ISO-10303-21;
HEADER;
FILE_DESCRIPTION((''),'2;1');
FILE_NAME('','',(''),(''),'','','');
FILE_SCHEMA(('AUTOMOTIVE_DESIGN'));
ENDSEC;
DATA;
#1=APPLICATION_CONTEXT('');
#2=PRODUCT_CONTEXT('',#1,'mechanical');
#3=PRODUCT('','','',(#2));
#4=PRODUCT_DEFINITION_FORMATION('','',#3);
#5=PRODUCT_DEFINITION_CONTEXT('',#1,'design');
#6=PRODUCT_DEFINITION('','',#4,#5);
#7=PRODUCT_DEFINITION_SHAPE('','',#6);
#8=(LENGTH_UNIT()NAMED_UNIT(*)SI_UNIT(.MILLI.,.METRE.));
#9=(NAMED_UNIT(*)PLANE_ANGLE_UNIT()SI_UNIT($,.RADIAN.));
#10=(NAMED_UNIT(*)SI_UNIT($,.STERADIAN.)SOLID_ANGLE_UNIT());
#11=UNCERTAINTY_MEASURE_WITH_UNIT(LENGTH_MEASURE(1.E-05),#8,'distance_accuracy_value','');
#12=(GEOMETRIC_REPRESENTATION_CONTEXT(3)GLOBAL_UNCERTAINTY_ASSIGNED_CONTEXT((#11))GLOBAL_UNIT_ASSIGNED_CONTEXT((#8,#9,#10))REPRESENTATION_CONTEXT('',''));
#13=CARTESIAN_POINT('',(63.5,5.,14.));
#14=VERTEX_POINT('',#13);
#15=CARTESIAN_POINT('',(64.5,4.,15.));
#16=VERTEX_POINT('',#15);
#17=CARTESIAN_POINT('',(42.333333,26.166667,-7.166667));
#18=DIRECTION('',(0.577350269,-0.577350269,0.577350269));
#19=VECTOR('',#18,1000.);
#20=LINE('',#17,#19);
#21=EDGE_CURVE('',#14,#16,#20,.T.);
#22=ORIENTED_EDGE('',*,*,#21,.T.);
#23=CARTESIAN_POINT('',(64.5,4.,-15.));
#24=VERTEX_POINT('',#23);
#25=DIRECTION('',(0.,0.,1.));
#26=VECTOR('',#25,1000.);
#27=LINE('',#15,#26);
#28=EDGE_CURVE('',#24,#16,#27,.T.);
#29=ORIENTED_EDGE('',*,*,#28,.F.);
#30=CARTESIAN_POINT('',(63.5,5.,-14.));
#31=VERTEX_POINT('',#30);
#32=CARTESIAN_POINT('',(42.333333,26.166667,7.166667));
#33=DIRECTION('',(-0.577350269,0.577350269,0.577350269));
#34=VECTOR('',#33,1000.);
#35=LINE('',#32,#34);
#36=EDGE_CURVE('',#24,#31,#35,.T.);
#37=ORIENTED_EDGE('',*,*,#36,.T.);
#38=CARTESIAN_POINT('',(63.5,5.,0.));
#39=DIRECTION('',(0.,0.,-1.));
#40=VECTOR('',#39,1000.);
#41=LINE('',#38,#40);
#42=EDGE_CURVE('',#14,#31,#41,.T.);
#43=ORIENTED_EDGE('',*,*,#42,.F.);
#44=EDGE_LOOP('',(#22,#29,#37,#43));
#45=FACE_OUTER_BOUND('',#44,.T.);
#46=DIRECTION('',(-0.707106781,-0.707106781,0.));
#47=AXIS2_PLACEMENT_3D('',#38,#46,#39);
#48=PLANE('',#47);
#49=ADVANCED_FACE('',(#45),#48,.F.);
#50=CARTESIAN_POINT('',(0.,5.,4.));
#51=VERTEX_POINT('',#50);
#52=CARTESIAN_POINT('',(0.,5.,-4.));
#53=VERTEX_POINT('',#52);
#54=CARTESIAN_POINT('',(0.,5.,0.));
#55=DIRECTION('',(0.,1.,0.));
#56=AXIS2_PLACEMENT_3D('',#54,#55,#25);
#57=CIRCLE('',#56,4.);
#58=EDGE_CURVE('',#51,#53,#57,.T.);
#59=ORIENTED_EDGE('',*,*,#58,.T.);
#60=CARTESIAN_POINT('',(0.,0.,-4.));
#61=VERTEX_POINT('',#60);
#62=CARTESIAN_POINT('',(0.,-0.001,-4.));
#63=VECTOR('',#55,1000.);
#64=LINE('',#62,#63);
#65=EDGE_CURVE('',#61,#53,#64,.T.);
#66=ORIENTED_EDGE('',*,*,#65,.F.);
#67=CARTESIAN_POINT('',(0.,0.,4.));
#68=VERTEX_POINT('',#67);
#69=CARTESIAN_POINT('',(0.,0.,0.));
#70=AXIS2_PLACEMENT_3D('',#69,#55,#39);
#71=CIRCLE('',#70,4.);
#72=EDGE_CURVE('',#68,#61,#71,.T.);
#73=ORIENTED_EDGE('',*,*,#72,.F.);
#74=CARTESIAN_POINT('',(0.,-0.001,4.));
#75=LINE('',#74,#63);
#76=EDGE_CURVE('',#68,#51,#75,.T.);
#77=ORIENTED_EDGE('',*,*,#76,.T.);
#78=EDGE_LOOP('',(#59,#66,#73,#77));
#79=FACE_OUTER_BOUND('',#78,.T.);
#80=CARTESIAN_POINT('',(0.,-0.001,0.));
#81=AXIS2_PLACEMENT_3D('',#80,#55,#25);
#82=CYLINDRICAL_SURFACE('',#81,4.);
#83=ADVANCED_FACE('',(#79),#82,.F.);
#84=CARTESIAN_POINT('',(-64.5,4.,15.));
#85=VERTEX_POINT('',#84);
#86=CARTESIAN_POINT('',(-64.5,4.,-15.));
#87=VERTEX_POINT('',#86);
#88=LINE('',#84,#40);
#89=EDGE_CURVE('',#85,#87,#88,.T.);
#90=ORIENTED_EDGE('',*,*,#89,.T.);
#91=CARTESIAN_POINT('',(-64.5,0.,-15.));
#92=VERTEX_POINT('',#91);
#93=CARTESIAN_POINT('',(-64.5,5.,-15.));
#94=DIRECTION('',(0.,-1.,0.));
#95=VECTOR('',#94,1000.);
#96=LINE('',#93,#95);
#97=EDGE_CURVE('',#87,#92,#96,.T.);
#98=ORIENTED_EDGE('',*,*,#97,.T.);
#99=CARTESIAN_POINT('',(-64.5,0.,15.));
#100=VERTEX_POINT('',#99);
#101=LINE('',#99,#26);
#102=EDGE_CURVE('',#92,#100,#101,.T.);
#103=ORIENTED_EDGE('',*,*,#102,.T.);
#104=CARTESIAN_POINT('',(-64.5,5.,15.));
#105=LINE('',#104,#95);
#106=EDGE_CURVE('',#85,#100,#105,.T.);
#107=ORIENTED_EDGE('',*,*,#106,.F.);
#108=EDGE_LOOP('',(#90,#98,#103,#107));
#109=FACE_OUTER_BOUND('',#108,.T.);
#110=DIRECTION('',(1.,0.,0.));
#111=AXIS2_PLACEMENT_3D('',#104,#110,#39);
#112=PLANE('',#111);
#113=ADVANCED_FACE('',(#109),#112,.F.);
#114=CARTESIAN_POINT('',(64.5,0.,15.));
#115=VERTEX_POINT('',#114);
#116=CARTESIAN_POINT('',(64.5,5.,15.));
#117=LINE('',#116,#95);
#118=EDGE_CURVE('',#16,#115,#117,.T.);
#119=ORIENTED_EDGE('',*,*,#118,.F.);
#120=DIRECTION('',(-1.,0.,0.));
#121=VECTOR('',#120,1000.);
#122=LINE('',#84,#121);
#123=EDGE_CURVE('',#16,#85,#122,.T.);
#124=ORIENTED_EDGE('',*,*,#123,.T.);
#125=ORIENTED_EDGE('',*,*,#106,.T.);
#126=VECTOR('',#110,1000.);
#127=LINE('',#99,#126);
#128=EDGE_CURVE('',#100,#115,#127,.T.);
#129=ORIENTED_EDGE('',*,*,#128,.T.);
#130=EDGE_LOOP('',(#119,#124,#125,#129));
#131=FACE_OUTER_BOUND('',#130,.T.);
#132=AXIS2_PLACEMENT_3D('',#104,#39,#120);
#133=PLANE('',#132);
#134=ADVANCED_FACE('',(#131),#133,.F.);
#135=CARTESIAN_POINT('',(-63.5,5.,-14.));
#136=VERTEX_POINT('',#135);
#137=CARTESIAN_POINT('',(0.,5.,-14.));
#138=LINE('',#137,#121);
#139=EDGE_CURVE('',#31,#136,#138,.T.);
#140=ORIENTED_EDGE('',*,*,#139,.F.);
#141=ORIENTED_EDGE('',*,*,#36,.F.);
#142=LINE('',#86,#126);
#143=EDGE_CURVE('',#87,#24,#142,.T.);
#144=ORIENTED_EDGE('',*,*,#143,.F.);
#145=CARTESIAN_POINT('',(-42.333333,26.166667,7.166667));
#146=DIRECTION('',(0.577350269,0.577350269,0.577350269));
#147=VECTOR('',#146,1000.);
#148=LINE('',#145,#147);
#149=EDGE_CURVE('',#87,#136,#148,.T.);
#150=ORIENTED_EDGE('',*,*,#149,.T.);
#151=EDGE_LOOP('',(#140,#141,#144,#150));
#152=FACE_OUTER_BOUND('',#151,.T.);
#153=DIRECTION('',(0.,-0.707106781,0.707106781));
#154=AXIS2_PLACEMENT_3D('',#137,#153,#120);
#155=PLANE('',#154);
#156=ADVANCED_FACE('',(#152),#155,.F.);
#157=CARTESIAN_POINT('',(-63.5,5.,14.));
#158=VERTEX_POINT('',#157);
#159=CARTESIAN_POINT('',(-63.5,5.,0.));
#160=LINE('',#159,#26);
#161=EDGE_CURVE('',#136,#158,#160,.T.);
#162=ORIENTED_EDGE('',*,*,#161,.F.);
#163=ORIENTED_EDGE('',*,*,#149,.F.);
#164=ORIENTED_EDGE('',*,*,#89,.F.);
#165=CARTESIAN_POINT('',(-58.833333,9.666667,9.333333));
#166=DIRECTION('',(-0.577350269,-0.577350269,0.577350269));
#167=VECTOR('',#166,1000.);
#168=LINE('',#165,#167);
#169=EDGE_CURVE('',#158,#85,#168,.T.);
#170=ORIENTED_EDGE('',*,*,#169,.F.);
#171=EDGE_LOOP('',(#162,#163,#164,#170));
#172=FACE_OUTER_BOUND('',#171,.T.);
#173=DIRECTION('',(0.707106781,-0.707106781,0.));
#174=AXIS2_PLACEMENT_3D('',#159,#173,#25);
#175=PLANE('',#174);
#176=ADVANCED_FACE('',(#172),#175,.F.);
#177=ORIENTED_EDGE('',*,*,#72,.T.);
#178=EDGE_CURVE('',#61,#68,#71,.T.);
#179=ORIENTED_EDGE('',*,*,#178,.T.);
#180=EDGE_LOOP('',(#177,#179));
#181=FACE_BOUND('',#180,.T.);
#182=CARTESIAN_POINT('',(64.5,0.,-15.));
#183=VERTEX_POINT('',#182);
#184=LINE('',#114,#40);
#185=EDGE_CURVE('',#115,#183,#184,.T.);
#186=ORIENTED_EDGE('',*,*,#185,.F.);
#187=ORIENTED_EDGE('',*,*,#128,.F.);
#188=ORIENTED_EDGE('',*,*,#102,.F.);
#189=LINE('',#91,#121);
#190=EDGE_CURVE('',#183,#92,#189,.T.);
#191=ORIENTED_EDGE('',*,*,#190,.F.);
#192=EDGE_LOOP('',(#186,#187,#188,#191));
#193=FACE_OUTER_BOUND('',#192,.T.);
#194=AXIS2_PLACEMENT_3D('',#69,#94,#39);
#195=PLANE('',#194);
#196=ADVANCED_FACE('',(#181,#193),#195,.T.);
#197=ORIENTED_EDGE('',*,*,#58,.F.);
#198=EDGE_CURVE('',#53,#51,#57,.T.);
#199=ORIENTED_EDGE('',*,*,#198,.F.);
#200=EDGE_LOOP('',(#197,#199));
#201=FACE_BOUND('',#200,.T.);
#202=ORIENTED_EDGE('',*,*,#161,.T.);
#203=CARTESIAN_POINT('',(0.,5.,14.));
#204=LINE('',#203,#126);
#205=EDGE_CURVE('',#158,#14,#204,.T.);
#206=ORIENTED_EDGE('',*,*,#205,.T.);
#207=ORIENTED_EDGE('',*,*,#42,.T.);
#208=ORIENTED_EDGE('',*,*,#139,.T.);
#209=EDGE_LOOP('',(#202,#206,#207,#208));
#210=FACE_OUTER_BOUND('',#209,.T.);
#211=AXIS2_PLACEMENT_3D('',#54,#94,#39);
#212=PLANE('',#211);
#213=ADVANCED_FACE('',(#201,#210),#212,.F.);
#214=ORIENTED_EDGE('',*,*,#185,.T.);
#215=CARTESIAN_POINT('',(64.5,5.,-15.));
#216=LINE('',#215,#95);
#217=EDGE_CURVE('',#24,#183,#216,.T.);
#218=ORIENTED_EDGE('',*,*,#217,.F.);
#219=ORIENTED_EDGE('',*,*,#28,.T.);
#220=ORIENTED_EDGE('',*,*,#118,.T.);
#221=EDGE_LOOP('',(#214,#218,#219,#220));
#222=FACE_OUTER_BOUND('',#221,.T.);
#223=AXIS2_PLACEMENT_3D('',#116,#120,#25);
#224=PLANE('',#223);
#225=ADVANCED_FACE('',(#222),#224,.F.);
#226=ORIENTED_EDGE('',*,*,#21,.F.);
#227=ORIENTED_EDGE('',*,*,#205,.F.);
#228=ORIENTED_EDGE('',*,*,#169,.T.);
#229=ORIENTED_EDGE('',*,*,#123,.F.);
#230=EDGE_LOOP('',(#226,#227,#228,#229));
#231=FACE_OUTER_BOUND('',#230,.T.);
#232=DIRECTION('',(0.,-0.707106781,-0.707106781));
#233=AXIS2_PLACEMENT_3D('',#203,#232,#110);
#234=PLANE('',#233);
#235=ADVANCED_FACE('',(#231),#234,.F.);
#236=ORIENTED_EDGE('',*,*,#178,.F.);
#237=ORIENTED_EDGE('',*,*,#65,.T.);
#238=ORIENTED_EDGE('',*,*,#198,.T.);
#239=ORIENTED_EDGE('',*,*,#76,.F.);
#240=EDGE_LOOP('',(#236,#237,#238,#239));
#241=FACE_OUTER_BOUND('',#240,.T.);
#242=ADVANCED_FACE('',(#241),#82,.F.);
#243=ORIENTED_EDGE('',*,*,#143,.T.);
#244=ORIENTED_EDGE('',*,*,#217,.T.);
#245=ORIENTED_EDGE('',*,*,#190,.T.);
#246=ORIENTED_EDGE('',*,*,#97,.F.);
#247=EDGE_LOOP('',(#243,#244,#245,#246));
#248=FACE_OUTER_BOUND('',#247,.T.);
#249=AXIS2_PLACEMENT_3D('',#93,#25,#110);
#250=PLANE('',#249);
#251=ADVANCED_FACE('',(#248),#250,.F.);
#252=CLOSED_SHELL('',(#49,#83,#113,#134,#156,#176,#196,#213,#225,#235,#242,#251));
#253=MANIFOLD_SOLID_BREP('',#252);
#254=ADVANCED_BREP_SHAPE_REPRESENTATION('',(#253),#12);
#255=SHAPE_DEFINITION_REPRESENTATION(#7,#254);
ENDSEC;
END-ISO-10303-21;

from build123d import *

# Parameters (mm, degrees)
SKETCH1_W           = 129
SKETCH1_H           = 30
BOSS_EXTRUDE1_DEPTH = 5
CUT_EXTRUDE1_REACH  = 68.41
SKETCH3_R           = 4
CHAMFER1_SIZE       = 1


with BuildPart() as part:
    # Sketch1 → Boss-Extrude1 (new body)
    with BuildSketch(Plane(origin=(0, 0, 0), x_dir=(1, 0, 0), z_dir=(0, 1, 0))):
        Rectangle(SKETCH1_W, SKETCH1_H)
    extrude(amount=BOSS_EXTRUDE1_DEPTH)

    # Sketch3 → Cut-Extrude1 (cut, up to next)
    with BuildSketch(Plane(origin=(0, 5, 0), x_dir=(1, 0, 0), z_dir=(0, 1, 0)), mode=Mode.PRIVATE) as cut_extrude1_sk1:
        with Locations(Location((0, 0, 0), (0, 0, 270))):
            Circle(SKETCH3_R)
    cut_extrude1_tool1 = extrude(cut_extrude1_sk1.sketch, amount=-CUT_EXTRUDE1_REACH, mode=Mode.PRIVATE) & part.part
    add(cut_extrude1_tool1.solids().sort_by_distance((0, 5, 0))[0], mode=Mode.SUBTRACT)

    # Chamfer1
    chamfer1_edges = [part.edges().sort_by_distance(p)[0] for p in [
        (-64.5, 5, 0),
        (0, 5, 15),
        (64.5, 5, 0),
        (0, 5, -15),
    ]]
    chamfer(chamfer1_edges, length=CHAMFER1_SIZE)


solid = part.part
